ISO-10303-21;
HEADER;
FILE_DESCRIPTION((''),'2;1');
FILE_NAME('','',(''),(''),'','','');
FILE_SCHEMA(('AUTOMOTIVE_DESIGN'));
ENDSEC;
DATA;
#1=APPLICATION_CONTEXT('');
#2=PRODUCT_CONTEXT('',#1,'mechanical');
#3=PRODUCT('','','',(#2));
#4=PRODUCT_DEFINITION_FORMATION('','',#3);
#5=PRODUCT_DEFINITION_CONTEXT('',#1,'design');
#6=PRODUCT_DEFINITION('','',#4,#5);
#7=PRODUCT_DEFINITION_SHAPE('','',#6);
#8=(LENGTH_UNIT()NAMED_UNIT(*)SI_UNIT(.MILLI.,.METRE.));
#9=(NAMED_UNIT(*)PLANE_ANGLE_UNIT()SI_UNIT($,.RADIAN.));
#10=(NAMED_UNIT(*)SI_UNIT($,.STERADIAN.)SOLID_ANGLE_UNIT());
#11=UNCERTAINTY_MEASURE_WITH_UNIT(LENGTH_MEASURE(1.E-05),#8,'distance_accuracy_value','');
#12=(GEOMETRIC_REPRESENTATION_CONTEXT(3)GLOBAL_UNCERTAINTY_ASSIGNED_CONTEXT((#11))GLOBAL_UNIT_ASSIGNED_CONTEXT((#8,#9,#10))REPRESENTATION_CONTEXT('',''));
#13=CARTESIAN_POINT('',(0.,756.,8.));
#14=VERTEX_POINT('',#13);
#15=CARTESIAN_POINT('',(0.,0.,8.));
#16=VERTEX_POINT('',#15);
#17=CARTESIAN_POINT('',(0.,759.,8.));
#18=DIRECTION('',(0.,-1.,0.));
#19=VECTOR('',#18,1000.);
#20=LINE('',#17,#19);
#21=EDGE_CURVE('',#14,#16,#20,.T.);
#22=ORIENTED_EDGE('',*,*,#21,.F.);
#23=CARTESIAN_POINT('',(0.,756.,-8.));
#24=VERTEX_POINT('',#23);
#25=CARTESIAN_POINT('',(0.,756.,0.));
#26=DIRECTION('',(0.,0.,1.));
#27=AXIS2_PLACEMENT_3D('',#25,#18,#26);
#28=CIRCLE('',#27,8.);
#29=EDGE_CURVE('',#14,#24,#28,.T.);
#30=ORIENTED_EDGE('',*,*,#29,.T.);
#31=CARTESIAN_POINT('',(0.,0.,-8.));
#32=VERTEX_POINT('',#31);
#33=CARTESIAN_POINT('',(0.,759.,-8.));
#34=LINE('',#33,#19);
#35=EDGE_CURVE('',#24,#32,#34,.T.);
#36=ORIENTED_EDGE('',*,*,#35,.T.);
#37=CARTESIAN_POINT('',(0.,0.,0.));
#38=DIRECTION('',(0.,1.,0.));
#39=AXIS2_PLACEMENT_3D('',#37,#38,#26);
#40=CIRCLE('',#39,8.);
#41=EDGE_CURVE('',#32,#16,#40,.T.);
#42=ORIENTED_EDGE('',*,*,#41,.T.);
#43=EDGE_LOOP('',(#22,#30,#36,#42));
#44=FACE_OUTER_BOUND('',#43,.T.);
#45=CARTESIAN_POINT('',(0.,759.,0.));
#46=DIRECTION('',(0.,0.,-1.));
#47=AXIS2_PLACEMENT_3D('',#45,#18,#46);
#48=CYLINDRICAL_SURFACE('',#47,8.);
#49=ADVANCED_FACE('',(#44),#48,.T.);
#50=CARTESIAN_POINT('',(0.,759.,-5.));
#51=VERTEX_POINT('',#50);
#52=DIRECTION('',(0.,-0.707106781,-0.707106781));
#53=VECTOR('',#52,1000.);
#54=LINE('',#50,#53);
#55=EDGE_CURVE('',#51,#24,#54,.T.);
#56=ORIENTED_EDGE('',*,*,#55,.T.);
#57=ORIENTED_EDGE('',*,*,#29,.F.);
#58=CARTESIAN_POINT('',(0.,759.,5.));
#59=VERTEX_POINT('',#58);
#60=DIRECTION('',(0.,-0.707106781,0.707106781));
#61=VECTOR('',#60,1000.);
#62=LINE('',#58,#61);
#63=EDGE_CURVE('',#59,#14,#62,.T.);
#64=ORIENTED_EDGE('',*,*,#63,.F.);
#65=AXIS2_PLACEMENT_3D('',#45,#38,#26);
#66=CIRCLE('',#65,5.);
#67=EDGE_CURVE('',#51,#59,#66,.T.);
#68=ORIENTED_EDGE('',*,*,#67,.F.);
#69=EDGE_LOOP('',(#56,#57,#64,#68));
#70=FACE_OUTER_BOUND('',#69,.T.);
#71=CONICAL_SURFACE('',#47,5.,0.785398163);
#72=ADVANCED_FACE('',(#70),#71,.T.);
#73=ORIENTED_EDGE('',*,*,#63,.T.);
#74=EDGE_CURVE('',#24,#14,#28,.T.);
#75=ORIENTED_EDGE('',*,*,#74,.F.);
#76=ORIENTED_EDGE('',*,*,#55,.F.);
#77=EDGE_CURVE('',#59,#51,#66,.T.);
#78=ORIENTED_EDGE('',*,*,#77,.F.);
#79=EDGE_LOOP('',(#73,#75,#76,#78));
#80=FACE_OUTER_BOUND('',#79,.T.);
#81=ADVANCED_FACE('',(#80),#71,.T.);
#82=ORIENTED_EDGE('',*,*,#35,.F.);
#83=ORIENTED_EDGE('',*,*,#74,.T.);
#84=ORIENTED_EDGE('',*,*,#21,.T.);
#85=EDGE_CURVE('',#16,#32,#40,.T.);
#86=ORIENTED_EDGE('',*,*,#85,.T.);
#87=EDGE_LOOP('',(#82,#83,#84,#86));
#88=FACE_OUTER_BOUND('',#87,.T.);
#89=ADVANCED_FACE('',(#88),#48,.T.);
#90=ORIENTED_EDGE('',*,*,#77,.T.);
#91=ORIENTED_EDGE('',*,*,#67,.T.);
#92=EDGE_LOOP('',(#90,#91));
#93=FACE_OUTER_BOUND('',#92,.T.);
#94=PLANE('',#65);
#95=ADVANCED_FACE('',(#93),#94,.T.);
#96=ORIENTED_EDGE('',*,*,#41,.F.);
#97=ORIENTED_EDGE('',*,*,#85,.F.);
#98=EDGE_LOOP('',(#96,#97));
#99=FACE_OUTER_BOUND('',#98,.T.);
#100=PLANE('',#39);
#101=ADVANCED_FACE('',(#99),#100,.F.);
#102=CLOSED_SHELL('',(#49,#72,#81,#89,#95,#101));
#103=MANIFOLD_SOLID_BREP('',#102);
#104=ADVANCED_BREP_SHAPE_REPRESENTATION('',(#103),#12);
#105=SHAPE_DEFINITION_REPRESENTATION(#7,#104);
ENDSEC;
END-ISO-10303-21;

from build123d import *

# Parameters (mm, degrees)
SKETCH1_R           = 8
BOSS_EXTRUDE1_DEPTH = 759
CHAMFER1_SIZE       = 3


with BuildPart() as part:
    # Sketch1 → Boss-Extrude1 (new body)
    with BuildSketch(Plane(origin=(0, 0, 0), x_dir=(1, 0, 0), z_dir=(0, 1, 0))):
        with Locations(Location((0, 0, 0), (0, 0, 270))):
            Circle(SKETCH1_R)
    extrude(amount=BOSS_EXTRUDE1_DEPTH)

    # Chamfer1
    chamfer1_edges = [part.edges().sort_by_distance(p)[0] for p in [
        (0, 759, -8),
    ]]
    chamfer(chamfer1_edges, length=CHAMFER1_SIZE)


solid = part.part
